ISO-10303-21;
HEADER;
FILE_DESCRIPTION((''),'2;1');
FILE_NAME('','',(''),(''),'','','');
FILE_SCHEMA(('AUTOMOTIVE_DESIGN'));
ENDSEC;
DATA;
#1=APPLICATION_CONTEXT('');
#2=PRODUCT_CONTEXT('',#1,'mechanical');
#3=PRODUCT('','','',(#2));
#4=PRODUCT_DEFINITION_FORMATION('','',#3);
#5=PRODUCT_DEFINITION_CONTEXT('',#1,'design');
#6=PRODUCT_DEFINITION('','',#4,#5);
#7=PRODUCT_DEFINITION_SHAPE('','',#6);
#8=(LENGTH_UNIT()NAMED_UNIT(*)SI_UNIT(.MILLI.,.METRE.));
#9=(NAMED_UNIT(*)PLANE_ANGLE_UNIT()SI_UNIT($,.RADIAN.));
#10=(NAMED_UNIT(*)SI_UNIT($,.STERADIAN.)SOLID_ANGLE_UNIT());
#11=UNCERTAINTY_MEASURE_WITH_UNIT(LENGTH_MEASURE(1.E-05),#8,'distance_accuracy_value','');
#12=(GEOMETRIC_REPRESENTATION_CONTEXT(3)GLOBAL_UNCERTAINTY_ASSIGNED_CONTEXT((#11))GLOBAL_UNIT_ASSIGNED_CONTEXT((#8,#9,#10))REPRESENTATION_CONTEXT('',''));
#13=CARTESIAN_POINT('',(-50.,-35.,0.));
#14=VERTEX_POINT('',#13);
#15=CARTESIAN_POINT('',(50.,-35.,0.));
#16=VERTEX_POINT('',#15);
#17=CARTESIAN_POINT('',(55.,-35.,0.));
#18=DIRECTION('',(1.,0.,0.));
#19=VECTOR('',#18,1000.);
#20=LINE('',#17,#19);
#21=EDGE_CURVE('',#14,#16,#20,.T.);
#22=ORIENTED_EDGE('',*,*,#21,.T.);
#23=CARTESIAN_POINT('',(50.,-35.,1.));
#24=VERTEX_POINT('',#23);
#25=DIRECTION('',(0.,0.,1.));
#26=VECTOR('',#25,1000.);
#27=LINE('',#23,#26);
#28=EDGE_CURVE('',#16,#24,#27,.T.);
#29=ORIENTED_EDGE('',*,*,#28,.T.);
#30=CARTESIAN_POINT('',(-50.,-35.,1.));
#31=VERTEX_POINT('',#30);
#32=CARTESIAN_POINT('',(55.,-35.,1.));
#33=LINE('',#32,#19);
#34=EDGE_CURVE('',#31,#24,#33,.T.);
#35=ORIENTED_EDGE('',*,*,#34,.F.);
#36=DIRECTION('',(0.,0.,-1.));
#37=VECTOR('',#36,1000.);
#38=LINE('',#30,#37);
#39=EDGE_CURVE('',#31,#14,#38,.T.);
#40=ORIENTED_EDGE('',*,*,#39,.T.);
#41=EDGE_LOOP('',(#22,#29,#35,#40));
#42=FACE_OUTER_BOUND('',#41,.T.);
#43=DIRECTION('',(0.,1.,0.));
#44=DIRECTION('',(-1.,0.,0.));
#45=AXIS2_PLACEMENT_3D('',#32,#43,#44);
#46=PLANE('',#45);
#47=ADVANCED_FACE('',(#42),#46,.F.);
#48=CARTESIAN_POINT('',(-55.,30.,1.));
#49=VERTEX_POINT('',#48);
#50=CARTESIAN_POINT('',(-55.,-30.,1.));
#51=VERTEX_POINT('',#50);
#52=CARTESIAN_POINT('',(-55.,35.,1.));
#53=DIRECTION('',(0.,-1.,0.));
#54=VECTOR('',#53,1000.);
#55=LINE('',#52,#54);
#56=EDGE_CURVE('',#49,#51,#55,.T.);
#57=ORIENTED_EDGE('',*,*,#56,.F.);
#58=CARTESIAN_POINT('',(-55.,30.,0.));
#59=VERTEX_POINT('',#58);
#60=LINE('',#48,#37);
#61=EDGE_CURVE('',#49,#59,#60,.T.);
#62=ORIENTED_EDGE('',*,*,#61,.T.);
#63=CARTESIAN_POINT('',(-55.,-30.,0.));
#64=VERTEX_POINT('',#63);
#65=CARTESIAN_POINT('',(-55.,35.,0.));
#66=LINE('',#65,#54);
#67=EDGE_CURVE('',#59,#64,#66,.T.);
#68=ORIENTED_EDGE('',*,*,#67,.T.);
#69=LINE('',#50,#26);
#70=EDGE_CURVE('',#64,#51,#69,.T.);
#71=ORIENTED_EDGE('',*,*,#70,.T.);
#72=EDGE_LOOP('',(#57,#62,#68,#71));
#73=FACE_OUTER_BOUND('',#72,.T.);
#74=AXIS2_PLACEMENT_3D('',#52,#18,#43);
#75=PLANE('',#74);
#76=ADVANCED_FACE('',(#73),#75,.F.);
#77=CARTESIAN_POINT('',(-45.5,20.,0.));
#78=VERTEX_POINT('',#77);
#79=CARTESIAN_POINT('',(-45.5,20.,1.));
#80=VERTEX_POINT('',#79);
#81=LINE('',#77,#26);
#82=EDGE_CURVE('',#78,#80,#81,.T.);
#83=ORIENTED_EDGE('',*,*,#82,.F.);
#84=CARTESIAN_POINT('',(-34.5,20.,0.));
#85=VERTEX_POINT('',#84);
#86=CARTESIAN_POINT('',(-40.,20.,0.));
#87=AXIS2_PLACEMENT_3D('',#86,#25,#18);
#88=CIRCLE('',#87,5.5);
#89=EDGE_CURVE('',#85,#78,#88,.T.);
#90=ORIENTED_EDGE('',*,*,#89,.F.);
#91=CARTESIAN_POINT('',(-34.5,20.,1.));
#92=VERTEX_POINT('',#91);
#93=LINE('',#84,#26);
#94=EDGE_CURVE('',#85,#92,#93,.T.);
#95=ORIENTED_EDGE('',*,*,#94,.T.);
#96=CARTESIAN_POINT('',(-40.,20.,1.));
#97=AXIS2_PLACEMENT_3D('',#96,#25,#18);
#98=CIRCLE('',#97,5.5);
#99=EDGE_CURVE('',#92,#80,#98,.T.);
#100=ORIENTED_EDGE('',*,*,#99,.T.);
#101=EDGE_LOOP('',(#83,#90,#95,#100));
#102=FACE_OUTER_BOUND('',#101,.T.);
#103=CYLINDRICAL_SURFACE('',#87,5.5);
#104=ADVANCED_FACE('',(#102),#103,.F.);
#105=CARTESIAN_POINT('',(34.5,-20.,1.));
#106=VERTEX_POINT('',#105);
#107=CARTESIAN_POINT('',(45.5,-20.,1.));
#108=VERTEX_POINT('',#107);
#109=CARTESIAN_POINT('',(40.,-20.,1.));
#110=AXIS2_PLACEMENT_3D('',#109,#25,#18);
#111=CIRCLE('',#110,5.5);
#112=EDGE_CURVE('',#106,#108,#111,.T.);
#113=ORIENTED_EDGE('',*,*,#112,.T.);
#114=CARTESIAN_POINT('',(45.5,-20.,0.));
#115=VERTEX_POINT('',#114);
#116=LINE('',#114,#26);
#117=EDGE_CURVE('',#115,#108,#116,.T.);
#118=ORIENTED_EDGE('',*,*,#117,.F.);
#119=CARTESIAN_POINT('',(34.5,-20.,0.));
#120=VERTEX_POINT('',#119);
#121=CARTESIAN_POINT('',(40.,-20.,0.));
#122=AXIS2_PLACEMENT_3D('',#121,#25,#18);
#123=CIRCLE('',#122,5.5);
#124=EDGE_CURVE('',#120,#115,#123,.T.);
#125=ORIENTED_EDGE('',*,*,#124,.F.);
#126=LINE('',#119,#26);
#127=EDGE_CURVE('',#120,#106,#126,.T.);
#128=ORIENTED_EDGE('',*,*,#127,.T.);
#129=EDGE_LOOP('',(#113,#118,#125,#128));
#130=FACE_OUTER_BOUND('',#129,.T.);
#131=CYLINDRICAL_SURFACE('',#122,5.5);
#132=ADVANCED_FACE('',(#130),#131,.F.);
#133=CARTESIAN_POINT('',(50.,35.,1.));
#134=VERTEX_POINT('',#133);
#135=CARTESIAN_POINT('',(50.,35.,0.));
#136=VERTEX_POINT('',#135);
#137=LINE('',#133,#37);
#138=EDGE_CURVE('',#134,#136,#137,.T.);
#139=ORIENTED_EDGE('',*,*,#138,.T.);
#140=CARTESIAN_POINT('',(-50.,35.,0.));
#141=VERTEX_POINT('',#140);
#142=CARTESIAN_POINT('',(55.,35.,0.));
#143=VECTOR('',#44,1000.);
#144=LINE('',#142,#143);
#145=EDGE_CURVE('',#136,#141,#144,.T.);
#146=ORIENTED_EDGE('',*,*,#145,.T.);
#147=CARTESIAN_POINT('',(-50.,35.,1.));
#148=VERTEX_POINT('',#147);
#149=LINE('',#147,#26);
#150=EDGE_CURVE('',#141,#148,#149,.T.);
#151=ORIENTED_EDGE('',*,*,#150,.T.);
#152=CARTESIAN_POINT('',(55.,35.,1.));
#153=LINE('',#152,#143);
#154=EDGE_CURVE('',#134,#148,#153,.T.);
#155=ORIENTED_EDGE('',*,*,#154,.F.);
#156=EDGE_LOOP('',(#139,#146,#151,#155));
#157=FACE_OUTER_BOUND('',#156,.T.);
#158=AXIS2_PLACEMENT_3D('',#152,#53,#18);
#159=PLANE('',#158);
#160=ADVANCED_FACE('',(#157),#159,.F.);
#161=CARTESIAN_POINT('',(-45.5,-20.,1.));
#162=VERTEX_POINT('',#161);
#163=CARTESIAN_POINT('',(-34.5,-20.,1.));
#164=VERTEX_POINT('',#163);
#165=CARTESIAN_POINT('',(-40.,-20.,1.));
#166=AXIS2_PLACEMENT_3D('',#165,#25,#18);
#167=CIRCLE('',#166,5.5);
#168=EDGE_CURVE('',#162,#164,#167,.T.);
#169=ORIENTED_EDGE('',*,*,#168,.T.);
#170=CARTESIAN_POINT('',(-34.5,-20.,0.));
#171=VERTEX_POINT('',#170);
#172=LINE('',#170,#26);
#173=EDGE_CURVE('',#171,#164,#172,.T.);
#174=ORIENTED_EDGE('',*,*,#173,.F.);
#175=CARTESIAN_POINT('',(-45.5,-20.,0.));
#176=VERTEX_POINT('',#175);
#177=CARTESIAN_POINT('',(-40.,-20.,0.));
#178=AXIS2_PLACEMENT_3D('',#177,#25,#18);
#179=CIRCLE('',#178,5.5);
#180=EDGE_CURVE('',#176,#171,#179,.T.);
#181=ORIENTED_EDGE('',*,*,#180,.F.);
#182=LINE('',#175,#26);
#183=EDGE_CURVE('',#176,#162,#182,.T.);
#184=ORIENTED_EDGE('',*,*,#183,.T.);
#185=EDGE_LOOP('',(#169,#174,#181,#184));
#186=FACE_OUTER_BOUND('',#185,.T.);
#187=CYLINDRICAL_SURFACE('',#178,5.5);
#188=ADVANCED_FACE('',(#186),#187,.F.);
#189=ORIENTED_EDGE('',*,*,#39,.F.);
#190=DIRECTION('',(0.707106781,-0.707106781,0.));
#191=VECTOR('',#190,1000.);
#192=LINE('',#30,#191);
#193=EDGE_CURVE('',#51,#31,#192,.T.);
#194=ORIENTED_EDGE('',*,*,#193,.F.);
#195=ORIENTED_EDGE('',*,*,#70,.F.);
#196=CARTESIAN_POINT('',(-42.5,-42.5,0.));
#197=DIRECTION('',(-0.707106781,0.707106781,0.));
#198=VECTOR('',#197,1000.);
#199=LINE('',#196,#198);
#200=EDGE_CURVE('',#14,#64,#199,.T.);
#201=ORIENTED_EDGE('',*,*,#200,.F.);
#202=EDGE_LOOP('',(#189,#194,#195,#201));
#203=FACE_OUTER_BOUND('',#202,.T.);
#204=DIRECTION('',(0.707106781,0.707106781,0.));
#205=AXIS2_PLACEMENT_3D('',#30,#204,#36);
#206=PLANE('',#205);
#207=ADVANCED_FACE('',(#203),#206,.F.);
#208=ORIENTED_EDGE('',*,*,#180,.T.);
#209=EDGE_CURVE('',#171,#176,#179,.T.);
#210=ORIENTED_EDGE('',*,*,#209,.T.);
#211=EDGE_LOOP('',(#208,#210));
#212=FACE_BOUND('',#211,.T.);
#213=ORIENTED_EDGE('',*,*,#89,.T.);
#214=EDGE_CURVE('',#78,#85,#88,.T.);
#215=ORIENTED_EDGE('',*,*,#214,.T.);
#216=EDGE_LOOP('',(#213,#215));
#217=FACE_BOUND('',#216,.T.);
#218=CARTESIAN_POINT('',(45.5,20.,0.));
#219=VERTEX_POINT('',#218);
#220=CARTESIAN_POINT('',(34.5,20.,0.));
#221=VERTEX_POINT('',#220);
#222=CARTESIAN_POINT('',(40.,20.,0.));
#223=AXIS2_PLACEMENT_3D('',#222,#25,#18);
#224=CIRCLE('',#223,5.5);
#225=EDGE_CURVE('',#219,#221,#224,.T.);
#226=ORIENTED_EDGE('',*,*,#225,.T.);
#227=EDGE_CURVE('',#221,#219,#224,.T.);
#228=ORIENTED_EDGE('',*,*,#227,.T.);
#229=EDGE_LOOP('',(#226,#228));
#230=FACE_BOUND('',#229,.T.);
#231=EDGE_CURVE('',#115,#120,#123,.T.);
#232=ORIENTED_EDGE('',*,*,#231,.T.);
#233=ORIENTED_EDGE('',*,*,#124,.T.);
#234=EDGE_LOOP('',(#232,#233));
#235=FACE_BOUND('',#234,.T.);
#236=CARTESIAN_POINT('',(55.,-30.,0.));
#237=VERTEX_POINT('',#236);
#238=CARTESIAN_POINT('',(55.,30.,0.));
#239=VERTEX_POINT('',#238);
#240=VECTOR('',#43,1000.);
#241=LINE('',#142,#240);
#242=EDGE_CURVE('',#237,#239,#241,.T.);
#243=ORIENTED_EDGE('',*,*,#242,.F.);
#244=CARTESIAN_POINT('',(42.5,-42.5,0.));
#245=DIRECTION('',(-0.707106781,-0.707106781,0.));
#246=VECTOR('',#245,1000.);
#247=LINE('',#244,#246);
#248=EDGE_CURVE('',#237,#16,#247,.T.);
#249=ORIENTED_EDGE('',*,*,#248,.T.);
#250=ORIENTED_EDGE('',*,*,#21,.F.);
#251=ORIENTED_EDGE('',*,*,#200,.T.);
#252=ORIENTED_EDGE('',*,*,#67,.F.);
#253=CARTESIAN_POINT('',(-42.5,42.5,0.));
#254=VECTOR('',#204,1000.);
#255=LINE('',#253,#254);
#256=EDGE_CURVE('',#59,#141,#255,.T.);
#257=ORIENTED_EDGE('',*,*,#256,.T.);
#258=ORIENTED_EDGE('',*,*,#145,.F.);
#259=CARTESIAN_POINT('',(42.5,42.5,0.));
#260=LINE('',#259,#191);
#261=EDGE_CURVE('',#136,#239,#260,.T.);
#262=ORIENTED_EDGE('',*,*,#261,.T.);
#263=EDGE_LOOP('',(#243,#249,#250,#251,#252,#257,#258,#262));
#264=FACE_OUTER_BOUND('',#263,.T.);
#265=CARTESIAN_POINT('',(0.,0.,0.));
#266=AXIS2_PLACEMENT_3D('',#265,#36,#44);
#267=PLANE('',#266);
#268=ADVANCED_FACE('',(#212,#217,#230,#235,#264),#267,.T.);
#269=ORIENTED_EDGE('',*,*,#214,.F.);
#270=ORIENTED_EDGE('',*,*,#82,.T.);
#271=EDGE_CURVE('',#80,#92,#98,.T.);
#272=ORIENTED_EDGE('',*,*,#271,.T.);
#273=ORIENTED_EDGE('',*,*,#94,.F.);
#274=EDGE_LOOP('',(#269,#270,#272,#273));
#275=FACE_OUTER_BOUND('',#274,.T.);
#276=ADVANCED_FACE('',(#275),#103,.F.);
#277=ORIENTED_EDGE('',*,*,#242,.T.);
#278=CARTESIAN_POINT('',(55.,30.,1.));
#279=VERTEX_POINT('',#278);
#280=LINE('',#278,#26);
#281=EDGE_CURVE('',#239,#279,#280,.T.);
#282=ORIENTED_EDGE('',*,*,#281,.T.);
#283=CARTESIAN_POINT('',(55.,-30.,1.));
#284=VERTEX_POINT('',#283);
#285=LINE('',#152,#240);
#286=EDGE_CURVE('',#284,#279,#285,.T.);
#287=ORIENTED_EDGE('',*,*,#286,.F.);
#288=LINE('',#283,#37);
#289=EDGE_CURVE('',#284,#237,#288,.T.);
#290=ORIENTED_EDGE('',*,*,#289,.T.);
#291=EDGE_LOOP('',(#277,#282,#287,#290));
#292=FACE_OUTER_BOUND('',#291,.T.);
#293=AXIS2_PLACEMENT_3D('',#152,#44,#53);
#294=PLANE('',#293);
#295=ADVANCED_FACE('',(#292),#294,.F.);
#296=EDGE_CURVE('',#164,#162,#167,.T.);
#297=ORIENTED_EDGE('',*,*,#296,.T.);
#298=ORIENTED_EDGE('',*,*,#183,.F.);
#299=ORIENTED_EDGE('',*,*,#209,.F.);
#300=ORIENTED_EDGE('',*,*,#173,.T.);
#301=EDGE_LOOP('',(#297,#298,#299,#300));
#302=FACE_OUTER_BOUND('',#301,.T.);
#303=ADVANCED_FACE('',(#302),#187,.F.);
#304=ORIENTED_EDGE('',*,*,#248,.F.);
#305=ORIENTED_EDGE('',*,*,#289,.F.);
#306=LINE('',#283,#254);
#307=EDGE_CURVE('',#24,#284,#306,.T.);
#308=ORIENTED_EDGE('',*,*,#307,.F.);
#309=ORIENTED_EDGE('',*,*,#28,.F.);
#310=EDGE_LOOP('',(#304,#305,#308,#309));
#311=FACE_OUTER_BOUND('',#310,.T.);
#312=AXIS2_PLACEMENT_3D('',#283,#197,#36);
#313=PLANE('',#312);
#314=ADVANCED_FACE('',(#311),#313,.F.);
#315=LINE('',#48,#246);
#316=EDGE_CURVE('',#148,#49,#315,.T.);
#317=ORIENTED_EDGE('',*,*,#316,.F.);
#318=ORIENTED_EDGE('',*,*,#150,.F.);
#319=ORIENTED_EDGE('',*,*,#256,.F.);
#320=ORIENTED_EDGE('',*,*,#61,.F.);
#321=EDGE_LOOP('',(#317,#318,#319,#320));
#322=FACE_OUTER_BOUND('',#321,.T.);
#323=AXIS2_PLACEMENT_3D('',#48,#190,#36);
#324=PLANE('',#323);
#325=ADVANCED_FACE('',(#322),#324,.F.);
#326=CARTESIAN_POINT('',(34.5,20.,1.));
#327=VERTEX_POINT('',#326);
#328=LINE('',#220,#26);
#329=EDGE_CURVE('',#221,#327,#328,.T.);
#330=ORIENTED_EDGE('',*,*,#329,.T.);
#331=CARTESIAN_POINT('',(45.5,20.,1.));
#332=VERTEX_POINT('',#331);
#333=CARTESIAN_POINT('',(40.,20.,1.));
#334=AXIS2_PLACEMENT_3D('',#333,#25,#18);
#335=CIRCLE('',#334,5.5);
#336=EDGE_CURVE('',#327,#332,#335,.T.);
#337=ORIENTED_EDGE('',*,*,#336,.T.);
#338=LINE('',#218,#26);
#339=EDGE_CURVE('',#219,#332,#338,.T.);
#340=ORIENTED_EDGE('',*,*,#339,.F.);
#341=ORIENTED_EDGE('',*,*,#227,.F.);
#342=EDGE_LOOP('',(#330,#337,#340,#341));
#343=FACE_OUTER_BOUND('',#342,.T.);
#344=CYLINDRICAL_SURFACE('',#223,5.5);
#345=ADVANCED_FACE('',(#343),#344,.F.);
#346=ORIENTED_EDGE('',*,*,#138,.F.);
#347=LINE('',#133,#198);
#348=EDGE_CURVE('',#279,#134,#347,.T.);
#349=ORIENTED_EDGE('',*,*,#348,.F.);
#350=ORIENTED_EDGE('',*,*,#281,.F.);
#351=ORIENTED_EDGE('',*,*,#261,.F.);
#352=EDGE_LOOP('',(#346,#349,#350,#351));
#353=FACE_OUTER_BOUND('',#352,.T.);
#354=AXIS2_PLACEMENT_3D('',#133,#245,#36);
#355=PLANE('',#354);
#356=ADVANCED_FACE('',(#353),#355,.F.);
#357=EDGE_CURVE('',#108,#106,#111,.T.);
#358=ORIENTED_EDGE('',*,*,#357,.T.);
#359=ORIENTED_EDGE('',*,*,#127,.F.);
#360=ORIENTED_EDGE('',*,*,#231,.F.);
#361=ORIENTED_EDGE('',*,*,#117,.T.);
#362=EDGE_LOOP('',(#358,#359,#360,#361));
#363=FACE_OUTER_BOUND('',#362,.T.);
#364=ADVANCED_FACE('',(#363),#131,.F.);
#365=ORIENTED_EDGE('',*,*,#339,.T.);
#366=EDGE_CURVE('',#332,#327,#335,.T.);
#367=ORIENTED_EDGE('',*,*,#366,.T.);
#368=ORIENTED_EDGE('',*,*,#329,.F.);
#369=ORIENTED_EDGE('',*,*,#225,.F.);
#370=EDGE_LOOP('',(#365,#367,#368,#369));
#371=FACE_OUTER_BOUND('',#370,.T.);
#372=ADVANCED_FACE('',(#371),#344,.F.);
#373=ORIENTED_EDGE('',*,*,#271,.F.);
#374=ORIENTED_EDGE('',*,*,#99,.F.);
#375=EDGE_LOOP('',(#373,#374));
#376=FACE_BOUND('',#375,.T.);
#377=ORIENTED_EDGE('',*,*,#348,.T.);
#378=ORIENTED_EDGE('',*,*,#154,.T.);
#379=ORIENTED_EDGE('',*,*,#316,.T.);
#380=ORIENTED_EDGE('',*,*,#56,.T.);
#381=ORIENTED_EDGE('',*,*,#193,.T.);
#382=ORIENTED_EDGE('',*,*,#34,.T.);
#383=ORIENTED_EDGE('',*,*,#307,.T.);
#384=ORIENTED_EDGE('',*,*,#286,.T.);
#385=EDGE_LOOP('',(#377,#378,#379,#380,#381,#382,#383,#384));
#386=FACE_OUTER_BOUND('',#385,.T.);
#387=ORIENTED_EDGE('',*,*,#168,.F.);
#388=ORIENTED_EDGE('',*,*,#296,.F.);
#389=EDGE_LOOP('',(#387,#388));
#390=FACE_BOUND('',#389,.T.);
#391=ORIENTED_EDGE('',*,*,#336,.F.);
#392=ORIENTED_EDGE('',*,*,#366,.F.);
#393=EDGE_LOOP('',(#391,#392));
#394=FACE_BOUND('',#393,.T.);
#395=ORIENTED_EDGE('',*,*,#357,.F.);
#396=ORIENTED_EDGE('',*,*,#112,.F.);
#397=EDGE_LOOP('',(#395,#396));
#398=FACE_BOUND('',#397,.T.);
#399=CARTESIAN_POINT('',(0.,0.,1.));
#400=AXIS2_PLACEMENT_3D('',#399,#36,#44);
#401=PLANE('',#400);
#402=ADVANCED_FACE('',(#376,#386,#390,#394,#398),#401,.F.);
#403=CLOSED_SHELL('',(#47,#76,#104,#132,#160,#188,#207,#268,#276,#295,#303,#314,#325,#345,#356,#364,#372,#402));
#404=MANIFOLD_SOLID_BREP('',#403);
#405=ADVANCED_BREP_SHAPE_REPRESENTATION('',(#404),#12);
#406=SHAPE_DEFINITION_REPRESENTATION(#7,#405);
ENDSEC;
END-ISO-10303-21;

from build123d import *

# Parameters (mm, degrees)
SKETCH1_W           = 110
SKETCH1_H           = 70
BOSS_EXTRUDE1_DEPTH = 1
SKETCH2_R           = 5.5
CUT_EXTRUDE1_DEPTH  = 1
CHAMFER1_SIZE       = 5


with BuildPart() as part:
    # Sketch1 → Boss-Extrude1 (new body)
    with BuildSketch(Plane.XY):
        Rectangle(SKETCH1_W, SKETCH1_H)
    extrude(amount=BOSS_EXTRUDE1_DEPTH)

    # Sketch2 → Cut-Extrude1 (cut)
    with BuildSketch(Plane.XY.offset(1)):
        with Locations((-40, 20)):
            Circle(SKETCH2_R)
        with Locations((40, 20)):
            Circle(SKETCH2_R)
        with Locations((-40, -20)):
            Circle(SKETCH2_R)
        with Locations((40, -20)):
            Circle(SKETCH2_R)
    extrude(amount=-CUT_EXTRUDE1_DEPTH, mode=Mode.SUBTRACT)

    # Chamfer1
    chamfer1_edges = [part.edges().sort_by_distance(p)[0] for p in [
        (-55, 35, 0.5),
        (55, 35, 0.5),
        (55, -35, 0.5),
        (-55, -35, 0.5),
    ]]
    chamfer(chamfer1_edges, length=CHAMFER1_SIZE)


solid = part.part
